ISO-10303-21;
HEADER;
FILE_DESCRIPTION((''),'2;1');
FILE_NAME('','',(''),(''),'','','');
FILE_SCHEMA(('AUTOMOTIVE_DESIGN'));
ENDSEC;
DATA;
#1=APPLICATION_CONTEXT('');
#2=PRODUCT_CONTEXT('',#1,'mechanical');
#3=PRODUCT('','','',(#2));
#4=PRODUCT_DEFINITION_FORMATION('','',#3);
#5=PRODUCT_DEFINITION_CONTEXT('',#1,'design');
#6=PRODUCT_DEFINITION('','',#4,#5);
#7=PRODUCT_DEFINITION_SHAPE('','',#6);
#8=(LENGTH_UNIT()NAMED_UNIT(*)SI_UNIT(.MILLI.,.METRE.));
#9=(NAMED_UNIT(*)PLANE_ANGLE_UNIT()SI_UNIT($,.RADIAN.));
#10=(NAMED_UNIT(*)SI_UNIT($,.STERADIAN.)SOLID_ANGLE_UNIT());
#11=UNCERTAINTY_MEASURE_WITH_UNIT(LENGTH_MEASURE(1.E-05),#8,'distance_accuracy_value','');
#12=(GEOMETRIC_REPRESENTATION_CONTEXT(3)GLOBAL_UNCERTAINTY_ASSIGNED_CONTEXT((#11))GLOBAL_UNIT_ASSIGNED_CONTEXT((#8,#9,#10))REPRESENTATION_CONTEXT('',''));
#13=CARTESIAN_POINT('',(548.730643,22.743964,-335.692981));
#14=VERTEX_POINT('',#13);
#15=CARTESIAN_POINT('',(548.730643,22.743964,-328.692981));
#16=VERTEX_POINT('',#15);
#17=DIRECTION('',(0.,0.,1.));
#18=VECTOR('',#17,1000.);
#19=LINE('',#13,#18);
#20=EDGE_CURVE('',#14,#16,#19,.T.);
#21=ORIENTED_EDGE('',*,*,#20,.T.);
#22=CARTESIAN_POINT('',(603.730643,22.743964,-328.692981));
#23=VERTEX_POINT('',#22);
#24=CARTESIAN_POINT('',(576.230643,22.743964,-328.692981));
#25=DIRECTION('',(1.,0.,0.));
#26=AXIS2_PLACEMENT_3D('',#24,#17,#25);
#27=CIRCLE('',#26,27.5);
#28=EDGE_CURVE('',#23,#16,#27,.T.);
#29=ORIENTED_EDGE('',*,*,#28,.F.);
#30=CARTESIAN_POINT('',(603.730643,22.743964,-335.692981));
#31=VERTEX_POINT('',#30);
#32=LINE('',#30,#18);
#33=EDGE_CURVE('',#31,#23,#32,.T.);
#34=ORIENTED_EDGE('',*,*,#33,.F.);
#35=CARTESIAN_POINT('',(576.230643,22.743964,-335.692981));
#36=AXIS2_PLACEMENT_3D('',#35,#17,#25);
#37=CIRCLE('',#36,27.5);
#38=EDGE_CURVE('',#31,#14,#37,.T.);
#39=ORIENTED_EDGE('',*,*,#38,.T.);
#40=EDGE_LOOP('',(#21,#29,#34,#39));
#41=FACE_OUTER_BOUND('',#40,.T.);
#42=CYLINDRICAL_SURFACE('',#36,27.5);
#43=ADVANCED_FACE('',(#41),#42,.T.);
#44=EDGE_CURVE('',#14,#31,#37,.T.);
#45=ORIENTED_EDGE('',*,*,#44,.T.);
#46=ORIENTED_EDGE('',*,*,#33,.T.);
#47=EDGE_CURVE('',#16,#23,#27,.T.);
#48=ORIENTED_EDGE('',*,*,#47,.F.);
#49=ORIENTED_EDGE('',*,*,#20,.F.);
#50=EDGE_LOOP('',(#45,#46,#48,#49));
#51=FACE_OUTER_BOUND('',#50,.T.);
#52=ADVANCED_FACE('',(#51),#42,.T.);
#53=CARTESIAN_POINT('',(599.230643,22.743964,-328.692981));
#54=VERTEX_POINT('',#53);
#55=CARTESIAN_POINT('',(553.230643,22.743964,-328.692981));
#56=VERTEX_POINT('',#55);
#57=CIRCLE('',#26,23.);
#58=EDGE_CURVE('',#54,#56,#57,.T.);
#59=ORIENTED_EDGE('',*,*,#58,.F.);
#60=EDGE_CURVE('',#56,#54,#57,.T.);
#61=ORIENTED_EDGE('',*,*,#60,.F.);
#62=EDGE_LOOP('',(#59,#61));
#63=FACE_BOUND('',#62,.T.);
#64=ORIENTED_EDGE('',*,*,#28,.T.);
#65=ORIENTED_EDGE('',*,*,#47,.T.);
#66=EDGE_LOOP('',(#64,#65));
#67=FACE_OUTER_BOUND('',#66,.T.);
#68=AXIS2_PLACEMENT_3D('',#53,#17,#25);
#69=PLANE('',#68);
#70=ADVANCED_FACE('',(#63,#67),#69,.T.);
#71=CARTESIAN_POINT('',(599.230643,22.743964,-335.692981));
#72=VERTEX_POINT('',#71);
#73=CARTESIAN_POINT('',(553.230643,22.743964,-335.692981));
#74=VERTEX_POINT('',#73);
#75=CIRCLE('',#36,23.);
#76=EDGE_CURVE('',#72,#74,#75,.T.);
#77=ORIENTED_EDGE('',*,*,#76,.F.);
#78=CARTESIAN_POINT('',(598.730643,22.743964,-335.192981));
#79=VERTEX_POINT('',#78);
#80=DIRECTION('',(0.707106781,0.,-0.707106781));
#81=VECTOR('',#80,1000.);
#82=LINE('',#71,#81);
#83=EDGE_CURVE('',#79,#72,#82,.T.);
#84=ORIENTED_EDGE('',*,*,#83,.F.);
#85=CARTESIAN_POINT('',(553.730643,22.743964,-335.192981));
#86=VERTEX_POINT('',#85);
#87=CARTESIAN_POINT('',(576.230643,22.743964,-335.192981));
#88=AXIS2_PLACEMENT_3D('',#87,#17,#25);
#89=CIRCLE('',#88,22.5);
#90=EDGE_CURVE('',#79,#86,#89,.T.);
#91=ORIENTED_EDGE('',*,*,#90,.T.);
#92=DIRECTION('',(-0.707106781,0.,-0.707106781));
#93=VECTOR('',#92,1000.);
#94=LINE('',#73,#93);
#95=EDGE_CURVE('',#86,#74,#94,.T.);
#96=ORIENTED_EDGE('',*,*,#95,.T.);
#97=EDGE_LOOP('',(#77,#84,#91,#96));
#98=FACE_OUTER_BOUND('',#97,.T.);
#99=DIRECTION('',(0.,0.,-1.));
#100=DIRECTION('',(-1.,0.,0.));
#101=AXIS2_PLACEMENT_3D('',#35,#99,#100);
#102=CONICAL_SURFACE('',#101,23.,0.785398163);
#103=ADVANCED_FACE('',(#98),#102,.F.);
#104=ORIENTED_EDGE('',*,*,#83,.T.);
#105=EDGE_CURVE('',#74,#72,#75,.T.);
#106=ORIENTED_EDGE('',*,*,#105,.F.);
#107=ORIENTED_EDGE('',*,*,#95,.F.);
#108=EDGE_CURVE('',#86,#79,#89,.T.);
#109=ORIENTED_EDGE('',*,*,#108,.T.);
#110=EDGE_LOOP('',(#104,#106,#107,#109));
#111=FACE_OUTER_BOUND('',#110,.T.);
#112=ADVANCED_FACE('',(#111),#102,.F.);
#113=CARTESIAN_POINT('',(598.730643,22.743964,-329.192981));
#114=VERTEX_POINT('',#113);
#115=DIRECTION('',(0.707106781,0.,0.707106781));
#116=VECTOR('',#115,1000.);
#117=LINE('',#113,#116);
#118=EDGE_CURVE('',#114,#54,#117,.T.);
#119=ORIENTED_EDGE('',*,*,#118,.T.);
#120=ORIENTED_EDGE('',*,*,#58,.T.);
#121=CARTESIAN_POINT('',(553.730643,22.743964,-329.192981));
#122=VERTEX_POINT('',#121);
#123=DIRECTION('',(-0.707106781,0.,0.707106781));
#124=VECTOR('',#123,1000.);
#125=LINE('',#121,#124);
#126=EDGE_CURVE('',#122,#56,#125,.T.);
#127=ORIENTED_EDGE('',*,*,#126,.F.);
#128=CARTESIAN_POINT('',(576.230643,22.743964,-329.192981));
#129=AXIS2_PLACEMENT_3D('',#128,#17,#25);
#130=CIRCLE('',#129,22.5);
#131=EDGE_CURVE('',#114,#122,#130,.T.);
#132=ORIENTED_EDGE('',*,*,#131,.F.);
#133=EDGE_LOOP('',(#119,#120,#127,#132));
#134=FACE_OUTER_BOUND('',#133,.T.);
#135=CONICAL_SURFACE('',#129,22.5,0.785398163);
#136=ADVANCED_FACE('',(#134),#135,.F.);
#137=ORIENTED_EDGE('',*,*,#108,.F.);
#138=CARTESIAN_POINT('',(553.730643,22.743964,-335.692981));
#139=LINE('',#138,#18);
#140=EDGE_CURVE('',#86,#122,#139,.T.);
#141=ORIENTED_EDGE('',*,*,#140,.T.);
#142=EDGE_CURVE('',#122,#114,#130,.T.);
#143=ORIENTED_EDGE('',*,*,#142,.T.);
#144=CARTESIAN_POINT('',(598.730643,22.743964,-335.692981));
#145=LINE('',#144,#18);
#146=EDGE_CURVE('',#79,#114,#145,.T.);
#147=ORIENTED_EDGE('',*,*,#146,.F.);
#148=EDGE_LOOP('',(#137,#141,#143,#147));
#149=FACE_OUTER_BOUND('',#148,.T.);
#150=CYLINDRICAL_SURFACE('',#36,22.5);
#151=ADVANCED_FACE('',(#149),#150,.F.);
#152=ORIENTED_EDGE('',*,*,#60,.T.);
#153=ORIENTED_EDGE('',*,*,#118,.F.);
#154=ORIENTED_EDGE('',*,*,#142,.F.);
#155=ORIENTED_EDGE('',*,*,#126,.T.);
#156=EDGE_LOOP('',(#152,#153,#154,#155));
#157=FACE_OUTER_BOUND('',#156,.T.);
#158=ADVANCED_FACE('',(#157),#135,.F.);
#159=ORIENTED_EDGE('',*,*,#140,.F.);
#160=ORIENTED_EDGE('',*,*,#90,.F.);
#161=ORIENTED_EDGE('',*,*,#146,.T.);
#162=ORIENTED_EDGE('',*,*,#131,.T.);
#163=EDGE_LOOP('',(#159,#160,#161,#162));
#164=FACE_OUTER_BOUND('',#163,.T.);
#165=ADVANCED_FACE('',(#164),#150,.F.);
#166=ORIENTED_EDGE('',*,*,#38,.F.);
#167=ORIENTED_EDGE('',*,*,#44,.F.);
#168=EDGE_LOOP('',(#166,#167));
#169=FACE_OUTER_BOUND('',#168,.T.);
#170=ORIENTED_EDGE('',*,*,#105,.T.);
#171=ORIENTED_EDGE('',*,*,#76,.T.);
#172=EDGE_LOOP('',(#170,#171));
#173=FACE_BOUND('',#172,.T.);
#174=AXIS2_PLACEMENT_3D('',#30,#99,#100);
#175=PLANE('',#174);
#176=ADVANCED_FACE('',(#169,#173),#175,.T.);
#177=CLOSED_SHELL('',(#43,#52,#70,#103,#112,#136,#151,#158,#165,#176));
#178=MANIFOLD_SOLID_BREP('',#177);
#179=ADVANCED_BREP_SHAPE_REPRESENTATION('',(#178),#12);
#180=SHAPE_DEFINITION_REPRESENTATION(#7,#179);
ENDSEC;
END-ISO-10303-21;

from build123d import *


with BuildPart() as part:
    # Sketch1 → Revolve1 (revolve)
    with BuildSketch(Plane(origin=(0, 22.743963655, 0), x_dir=(1, 0, 0), z_dir=(0, 1, 0))):
        Polygon((598.730642584, 329.192981355), (599.230642584, 328.692981355), (603.730642584, 328.692981355), (603.730642584, 335.692981355), (599.230642584, 335.692981355), (598.730642584, 335.192981355), align=None)
    revolve(axis=Axis((576.230642584, 22.743963655, -335.692981355), (0, 0, 1)))


solid = part.part
